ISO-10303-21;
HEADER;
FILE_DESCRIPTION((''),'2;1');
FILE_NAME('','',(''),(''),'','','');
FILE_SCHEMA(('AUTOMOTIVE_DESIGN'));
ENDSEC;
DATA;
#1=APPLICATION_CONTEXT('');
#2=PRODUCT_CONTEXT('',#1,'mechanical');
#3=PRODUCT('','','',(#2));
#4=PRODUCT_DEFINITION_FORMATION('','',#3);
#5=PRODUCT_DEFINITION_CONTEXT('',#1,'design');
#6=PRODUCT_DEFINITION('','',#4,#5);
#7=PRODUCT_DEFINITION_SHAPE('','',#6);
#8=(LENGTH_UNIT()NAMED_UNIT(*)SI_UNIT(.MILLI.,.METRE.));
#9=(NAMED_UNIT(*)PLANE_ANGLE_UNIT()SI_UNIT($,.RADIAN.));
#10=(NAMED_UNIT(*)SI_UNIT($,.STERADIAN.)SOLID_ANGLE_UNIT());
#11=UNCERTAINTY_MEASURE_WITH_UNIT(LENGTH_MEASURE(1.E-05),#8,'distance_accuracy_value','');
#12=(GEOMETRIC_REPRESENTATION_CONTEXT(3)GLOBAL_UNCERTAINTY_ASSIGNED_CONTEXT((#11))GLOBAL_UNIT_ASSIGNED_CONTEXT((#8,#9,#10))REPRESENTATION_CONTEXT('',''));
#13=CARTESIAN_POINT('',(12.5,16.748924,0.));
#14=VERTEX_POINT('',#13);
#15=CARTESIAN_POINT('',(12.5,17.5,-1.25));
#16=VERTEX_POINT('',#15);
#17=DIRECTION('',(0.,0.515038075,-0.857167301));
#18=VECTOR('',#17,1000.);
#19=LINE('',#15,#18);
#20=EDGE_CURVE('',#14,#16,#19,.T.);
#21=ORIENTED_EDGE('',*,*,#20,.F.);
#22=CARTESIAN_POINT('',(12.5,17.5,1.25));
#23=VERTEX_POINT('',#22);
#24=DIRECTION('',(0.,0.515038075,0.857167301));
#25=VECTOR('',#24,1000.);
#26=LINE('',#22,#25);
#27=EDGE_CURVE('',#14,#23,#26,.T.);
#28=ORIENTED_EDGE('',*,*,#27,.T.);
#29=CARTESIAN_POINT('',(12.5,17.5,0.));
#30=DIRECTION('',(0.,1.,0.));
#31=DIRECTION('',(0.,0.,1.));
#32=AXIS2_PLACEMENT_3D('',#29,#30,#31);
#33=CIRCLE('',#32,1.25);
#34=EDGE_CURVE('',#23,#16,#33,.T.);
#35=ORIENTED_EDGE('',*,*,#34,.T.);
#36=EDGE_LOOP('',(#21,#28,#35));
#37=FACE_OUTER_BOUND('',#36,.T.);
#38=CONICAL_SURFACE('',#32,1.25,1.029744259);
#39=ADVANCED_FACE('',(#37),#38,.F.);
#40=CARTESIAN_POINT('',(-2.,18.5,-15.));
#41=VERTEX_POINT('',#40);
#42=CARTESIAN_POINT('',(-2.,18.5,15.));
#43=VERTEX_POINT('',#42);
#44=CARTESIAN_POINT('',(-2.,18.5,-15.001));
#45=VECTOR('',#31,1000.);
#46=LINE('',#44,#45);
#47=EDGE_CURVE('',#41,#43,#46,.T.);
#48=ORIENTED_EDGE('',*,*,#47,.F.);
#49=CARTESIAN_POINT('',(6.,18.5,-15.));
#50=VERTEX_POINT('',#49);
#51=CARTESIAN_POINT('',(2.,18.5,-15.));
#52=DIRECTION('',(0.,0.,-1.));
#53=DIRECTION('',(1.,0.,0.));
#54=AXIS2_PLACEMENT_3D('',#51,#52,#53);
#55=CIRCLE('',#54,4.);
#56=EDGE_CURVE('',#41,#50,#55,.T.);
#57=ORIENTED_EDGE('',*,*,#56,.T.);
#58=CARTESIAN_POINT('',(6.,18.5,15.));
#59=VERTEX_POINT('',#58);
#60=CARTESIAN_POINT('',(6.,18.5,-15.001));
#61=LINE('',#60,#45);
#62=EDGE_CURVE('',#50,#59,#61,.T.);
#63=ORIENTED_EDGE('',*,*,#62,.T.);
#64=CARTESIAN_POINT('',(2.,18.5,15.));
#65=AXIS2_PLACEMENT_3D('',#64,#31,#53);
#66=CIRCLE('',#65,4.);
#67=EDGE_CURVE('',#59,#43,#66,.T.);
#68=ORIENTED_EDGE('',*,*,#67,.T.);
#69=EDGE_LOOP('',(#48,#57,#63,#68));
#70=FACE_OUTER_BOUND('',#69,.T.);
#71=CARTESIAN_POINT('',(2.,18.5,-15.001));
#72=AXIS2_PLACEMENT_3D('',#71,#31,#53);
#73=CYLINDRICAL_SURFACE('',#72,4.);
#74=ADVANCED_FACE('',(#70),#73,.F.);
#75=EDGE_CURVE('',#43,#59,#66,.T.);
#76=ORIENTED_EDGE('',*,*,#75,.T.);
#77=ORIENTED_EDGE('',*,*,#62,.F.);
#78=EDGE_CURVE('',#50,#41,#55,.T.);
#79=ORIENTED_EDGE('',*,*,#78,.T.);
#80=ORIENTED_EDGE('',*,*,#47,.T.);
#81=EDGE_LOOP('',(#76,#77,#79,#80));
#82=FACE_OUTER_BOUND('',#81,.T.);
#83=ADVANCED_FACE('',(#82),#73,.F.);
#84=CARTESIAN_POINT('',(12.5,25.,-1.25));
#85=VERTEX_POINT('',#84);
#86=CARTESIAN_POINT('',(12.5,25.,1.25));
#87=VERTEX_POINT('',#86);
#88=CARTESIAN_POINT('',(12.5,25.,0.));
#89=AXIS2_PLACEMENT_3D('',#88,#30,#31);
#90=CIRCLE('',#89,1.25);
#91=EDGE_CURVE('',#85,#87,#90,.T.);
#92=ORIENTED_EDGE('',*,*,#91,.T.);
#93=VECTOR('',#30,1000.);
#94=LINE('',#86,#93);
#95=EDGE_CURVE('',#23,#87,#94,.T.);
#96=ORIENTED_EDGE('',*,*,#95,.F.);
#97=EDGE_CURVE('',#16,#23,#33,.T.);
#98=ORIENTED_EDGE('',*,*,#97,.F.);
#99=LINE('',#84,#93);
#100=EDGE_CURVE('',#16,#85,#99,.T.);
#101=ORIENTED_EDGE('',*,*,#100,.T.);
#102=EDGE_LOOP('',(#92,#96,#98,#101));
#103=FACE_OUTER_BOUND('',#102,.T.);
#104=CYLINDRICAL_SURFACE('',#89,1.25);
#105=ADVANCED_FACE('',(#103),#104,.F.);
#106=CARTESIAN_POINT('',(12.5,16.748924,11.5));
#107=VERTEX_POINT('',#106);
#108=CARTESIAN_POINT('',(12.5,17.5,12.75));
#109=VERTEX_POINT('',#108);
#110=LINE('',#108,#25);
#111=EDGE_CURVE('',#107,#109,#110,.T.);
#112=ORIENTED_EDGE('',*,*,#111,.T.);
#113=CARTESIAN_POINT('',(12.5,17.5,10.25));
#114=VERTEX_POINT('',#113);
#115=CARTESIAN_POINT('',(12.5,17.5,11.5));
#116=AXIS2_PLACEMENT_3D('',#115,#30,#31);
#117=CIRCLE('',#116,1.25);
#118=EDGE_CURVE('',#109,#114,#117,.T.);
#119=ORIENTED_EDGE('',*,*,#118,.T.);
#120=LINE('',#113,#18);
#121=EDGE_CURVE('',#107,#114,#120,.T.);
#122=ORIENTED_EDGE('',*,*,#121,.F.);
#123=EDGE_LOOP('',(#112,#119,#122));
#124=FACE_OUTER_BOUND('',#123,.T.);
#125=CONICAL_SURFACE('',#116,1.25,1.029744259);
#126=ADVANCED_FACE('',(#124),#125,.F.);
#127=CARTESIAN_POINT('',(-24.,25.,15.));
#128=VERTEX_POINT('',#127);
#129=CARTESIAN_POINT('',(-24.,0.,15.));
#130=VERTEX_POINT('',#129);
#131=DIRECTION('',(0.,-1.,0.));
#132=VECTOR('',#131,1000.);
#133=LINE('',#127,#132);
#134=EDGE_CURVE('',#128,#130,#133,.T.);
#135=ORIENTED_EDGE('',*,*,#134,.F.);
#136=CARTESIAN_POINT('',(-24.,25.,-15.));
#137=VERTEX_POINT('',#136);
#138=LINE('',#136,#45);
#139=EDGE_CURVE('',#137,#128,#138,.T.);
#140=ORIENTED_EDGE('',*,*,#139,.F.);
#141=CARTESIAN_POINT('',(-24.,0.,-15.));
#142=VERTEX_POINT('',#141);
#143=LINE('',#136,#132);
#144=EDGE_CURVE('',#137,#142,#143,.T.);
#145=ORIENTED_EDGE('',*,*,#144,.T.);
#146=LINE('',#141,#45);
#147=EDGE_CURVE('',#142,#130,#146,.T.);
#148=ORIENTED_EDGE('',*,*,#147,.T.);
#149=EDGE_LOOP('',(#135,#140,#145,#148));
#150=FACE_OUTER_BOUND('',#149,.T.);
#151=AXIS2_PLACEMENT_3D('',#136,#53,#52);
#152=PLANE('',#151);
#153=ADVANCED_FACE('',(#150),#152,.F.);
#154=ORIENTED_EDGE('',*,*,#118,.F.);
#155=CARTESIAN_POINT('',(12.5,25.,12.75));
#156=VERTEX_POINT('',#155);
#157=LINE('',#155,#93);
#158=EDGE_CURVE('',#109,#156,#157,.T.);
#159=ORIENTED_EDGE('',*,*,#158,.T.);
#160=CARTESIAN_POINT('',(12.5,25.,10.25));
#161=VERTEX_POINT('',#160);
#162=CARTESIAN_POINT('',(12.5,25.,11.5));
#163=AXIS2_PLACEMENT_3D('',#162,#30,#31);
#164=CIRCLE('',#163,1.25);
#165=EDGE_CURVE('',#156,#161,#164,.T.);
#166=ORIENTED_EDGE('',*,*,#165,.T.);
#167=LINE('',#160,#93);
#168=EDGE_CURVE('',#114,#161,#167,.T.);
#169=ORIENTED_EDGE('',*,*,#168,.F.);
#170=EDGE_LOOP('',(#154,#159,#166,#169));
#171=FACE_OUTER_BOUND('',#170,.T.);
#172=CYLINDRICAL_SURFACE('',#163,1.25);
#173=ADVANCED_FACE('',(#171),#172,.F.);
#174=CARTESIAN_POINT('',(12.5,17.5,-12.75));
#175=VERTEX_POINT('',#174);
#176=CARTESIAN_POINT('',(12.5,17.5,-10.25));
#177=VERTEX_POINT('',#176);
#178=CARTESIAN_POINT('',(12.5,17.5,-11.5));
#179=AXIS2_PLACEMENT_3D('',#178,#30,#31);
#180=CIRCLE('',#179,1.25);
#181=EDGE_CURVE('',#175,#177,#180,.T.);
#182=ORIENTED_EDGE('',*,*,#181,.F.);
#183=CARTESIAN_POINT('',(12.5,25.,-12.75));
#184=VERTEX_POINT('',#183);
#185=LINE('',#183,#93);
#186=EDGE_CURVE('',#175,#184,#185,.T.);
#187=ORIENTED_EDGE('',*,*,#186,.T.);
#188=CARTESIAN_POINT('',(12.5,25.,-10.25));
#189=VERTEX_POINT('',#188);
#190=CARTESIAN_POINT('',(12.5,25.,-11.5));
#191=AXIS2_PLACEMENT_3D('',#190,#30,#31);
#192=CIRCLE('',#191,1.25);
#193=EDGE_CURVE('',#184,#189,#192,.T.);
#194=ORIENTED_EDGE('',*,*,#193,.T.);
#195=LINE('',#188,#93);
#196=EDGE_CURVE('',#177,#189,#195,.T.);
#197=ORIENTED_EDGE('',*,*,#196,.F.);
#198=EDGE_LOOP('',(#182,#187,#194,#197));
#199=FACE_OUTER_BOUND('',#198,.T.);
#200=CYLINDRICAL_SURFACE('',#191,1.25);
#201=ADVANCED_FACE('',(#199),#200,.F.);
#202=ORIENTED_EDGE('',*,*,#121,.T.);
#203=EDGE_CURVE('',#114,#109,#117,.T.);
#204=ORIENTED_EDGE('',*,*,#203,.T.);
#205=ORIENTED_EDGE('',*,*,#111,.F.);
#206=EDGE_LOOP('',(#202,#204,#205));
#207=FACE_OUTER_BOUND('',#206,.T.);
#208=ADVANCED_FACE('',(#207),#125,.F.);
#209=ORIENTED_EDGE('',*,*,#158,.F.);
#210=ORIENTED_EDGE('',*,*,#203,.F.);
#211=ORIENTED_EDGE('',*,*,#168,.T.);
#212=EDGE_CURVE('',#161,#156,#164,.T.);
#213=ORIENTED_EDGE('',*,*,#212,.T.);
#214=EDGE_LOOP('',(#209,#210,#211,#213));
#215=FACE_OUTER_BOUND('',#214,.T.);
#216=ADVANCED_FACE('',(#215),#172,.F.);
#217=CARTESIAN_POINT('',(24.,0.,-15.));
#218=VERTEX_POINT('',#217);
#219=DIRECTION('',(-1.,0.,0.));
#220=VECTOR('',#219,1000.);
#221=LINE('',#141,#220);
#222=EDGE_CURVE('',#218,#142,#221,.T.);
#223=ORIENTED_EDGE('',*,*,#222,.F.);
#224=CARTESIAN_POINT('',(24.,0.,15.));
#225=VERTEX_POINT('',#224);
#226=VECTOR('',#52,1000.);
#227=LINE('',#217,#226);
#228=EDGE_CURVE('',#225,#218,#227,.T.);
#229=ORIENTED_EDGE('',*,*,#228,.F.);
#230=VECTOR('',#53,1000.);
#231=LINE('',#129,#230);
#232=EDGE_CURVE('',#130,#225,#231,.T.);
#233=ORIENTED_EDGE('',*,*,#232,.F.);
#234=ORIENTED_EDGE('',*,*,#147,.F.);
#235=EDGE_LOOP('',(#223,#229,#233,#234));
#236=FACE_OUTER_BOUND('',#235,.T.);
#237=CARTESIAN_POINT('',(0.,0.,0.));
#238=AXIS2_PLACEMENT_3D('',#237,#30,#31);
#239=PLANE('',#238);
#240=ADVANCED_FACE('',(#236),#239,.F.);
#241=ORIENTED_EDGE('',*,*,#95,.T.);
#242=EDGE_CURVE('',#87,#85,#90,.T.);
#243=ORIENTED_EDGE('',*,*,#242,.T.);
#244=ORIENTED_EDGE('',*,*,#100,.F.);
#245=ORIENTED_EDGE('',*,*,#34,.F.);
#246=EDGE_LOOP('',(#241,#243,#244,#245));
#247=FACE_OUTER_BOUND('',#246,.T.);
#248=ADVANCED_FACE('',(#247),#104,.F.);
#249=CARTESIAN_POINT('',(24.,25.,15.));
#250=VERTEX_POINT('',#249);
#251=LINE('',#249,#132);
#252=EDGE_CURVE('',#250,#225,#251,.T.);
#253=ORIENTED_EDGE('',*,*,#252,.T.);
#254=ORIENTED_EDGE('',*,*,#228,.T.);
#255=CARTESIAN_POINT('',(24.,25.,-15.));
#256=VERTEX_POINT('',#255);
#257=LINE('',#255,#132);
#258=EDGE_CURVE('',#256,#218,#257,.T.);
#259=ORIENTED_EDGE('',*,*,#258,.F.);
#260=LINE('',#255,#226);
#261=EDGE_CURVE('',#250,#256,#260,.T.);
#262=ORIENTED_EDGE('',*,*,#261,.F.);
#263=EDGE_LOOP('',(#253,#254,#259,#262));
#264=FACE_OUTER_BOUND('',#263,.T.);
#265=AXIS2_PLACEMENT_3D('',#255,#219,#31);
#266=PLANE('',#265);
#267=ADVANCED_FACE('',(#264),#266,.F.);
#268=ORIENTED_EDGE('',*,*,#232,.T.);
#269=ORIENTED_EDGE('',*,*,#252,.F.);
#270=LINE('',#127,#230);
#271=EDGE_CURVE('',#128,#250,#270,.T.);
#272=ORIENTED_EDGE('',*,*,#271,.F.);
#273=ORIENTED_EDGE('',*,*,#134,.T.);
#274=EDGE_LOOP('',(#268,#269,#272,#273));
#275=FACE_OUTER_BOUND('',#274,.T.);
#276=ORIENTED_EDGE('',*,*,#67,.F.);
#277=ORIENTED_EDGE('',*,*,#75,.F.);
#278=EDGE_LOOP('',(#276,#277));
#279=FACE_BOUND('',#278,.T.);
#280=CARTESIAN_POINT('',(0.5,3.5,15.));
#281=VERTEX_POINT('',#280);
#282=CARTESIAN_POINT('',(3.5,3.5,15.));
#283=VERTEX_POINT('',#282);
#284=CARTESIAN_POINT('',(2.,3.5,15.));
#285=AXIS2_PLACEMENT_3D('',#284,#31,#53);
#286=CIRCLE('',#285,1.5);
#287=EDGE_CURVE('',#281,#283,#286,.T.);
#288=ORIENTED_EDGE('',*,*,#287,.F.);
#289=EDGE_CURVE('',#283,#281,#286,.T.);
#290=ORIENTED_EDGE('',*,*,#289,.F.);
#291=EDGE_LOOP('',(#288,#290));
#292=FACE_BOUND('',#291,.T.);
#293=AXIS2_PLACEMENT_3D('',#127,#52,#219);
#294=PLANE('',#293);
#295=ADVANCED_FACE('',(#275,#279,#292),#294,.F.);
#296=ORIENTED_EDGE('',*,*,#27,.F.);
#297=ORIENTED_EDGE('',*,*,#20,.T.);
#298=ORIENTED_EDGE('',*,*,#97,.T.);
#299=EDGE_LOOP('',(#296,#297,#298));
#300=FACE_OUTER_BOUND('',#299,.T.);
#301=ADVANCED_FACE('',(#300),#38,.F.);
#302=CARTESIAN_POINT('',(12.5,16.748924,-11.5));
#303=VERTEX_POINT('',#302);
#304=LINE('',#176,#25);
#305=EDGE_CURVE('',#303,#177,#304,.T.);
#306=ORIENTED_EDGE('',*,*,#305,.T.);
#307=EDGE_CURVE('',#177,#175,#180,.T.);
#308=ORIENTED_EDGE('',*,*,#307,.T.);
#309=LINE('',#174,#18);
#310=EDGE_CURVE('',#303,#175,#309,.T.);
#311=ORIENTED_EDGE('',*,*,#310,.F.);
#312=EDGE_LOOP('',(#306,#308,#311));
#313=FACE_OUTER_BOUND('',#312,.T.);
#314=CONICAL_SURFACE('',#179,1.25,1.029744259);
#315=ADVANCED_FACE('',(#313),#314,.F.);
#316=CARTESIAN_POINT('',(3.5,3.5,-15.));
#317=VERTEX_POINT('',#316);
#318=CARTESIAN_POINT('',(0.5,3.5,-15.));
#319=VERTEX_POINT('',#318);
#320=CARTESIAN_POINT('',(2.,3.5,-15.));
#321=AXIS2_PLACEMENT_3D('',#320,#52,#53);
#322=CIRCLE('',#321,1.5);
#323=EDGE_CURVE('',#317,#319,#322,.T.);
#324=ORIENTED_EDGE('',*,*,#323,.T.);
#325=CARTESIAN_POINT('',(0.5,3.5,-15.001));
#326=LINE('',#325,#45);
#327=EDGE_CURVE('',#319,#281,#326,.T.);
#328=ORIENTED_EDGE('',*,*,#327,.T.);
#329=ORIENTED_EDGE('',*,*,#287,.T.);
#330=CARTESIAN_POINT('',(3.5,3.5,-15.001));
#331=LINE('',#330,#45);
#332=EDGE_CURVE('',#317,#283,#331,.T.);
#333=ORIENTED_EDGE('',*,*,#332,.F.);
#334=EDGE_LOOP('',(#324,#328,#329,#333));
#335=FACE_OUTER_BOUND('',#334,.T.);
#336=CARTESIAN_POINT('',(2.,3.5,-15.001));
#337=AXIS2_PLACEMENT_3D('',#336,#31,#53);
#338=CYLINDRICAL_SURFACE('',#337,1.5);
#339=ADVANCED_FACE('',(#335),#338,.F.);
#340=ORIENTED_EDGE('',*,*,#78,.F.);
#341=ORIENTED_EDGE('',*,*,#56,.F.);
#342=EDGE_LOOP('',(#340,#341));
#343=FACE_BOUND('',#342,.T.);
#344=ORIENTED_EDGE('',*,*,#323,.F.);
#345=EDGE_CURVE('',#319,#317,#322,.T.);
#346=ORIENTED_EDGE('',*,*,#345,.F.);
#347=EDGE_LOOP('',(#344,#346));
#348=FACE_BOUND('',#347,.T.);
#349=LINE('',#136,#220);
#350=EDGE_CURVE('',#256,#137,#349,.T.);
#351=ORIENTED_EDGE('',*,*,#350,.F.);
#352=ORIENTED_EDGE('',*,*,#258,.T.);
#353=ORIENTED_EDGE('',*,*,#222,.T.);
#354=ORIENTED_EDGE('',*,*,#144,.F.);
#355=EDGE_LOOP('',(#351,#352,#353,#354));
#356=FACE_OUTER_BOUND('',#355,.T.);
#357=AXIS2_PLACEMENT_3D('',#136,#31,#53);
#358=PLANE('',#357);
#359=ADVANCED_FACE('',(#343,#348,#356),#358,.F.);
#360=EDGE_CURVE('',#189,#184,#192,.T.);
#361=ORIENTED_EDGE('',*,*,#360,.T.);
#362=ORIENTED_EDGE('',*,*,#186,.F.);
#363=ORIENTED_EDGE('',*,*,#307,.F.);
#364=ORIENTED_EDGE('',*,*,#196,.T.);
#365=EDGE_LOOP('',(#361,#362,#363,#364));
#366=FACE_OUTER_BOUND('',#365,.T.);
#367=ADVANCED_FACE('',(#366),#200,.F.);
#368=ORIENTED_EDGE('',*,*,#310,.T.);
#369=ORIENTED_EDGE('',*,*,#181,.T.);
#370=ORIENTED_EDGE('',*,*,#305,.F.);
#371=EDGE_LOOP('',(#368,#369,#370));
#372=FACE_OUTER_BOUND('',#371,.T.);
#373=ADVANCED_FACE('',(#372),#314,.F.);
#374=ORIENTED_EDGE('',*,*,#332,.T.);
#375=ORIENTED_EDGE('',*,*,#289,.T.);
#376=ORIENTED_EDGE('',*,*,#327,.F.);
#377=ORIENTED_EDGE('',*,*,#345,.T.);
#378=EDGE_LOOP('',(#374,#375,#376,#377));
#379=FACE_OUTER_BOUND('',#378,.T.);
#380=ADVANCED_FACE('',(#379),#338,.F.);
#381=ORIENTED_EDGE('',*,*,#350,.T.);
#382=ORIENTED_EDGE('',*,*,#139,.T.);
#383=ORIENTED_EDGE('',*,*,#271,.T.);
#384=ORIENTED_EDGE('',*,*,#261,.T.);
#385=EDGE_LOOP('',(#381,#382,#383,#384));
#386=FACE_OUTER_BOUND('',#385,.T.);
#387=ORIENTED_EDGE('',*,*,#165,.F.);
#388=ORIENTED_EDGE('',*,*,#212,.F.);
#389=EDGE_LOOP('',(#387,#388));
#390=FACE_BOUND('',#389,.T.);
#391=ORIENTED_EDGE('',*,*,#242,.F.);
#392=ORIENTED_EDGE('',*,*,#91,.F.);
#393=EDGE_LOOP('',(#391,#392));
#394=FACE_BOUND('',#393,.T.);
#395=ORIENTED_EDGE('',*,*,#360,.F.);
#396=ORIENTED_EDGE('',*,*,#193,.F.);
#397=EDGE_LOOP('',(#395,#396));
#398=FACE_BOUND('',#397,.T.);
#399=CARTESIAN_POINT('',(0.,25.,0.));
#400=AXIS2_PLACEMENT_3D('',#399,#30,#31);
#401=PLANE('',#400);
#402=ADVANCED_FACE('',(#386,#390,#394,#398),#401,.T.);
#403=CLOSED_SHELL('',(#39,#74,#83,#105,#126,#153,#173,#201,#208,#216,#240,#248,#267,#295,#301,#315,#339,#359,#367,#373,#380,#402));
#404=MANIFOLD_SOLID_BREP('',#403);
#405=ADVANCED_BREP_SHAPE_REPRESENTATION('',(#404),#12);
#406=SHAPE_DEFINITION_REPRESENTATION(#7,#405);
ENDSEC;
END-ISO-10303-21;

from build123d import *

# Parameters (mm, degrees)
SKETCH1_W             = 48
SKETCH1_H             = 30
BOSS_EXTRUDE1_DEPTH   = 25
CUT_EXTRUDE2_REACH    = 47.837
SKETCH3_R             = 4
SKETCH3_R_2           = 1.5
SKETCH4_R             = 1
CUT_EXTRUDE3_DEPTH    = 2
M3_TAPPED_HOLE1_D     = 2.5
M3_TAPPED_HOLE1_DEPTH = 7.5
M3_TAPPED_HOLE1_TIP   = 0.751075774


with BuildPart() as part:
    # Sketch1 → Boss-Extrude1 (new body)
    with BuildSketch(Plane(origin=(0, 0, 0), x_dir=(1, 0, 0), z_dir=(0, 1, 0))):
        Rectangle(SKETCH1_W, SKETCH1_H)
    extrude(amount=BOSS_EXTRUDE1_DEPTH)

    # Sketch3 → Cut-Extrude2 (cut, up to next)
    with BuildSketch(Plane.XY.offset(15), mode=Mode.PRIVATE) as cut_extrude2_sk1:
        with Locations((2, 18.5)):
            Circle(SKETCH3_R)
    cut_extrude2_tool1 = extrude(cut_extrude2_sk1.sketch, amount=-CUT_EXTRUDE2_REACH, mode=Mode.PRIVATE) & part.part
    # Sketch3 → Cut-Extrude2 (cut, up to next)
    with BuildSketch(Plane.XY.offset(15), mode=Mode.PRIVATE) as cut_extrude2_sk2:
        with Locations((2, 3.5)):
            Circle(SKETCH3_R_2)
    cut_extrude2_tool2 = extrude(cut_extrude2_sk2.sketch, amount=-CUT_EXTRUDE2_REACH, mode=Mode.PRIVATE) & part.part
    add(cut_extrude2_tool1.solids().sort_by_distance((2, 18.5, 15))[0], mode=Mode.SUBTRACT)
    add(cut_extrude2_tool2.solids().sort_by_distance((2, 3.5, 15))[0], mode=Mode.SUBTRACT)

    # Sketch4 → Cut-Extrude3 (cut)
    with BuildSketch(Plane(origin=(0, 25, 0), x_dir=(1, 0, 0), z_dir=(0, 1, 0))):
        with Locations(Location((12.5, 11.5, 0), (0, 0, 270))):
            Circle(SKETCH4_R)
        with Locations(Location((12.5, 0, 0), (0, 0, 270))):
            Circle(SKETCH4_R)
        with Locations(Location((12.5, -11.5, 0), (0, 0, 270))):
            Circle(SKETCH4_R)
    extrude(amount=-CUT_EXTRUDE3_DEPTH, mode=Mode.SUBTRACT)

    # M3 Tapped Hole1
    with Locations(Plane(origin=(0, 25, 0), x_dir=(1, 0, 0), z_dir=(0, 1, 0))):
        with Locations((12.5, 11.5), (12.5, 0), (12.5, -11.5)):
            Hole(M3_TAPPED_HOLE1_D / 2, depth=M3_TAPPED_HOLE1_DEPTH)
            with Locations((0, 0, -(M3_TAPPED_HOLE1_DEPTH + M3_TAPPED_HOLE1_TIP / 2))):  # 118° drill point
                Cone(0, M3_TAPPED_HOLE1_D / 2, M3_TAPPED_HOLE1_TIP, mode=Mode.SUBTRACT)


solid = part.part
